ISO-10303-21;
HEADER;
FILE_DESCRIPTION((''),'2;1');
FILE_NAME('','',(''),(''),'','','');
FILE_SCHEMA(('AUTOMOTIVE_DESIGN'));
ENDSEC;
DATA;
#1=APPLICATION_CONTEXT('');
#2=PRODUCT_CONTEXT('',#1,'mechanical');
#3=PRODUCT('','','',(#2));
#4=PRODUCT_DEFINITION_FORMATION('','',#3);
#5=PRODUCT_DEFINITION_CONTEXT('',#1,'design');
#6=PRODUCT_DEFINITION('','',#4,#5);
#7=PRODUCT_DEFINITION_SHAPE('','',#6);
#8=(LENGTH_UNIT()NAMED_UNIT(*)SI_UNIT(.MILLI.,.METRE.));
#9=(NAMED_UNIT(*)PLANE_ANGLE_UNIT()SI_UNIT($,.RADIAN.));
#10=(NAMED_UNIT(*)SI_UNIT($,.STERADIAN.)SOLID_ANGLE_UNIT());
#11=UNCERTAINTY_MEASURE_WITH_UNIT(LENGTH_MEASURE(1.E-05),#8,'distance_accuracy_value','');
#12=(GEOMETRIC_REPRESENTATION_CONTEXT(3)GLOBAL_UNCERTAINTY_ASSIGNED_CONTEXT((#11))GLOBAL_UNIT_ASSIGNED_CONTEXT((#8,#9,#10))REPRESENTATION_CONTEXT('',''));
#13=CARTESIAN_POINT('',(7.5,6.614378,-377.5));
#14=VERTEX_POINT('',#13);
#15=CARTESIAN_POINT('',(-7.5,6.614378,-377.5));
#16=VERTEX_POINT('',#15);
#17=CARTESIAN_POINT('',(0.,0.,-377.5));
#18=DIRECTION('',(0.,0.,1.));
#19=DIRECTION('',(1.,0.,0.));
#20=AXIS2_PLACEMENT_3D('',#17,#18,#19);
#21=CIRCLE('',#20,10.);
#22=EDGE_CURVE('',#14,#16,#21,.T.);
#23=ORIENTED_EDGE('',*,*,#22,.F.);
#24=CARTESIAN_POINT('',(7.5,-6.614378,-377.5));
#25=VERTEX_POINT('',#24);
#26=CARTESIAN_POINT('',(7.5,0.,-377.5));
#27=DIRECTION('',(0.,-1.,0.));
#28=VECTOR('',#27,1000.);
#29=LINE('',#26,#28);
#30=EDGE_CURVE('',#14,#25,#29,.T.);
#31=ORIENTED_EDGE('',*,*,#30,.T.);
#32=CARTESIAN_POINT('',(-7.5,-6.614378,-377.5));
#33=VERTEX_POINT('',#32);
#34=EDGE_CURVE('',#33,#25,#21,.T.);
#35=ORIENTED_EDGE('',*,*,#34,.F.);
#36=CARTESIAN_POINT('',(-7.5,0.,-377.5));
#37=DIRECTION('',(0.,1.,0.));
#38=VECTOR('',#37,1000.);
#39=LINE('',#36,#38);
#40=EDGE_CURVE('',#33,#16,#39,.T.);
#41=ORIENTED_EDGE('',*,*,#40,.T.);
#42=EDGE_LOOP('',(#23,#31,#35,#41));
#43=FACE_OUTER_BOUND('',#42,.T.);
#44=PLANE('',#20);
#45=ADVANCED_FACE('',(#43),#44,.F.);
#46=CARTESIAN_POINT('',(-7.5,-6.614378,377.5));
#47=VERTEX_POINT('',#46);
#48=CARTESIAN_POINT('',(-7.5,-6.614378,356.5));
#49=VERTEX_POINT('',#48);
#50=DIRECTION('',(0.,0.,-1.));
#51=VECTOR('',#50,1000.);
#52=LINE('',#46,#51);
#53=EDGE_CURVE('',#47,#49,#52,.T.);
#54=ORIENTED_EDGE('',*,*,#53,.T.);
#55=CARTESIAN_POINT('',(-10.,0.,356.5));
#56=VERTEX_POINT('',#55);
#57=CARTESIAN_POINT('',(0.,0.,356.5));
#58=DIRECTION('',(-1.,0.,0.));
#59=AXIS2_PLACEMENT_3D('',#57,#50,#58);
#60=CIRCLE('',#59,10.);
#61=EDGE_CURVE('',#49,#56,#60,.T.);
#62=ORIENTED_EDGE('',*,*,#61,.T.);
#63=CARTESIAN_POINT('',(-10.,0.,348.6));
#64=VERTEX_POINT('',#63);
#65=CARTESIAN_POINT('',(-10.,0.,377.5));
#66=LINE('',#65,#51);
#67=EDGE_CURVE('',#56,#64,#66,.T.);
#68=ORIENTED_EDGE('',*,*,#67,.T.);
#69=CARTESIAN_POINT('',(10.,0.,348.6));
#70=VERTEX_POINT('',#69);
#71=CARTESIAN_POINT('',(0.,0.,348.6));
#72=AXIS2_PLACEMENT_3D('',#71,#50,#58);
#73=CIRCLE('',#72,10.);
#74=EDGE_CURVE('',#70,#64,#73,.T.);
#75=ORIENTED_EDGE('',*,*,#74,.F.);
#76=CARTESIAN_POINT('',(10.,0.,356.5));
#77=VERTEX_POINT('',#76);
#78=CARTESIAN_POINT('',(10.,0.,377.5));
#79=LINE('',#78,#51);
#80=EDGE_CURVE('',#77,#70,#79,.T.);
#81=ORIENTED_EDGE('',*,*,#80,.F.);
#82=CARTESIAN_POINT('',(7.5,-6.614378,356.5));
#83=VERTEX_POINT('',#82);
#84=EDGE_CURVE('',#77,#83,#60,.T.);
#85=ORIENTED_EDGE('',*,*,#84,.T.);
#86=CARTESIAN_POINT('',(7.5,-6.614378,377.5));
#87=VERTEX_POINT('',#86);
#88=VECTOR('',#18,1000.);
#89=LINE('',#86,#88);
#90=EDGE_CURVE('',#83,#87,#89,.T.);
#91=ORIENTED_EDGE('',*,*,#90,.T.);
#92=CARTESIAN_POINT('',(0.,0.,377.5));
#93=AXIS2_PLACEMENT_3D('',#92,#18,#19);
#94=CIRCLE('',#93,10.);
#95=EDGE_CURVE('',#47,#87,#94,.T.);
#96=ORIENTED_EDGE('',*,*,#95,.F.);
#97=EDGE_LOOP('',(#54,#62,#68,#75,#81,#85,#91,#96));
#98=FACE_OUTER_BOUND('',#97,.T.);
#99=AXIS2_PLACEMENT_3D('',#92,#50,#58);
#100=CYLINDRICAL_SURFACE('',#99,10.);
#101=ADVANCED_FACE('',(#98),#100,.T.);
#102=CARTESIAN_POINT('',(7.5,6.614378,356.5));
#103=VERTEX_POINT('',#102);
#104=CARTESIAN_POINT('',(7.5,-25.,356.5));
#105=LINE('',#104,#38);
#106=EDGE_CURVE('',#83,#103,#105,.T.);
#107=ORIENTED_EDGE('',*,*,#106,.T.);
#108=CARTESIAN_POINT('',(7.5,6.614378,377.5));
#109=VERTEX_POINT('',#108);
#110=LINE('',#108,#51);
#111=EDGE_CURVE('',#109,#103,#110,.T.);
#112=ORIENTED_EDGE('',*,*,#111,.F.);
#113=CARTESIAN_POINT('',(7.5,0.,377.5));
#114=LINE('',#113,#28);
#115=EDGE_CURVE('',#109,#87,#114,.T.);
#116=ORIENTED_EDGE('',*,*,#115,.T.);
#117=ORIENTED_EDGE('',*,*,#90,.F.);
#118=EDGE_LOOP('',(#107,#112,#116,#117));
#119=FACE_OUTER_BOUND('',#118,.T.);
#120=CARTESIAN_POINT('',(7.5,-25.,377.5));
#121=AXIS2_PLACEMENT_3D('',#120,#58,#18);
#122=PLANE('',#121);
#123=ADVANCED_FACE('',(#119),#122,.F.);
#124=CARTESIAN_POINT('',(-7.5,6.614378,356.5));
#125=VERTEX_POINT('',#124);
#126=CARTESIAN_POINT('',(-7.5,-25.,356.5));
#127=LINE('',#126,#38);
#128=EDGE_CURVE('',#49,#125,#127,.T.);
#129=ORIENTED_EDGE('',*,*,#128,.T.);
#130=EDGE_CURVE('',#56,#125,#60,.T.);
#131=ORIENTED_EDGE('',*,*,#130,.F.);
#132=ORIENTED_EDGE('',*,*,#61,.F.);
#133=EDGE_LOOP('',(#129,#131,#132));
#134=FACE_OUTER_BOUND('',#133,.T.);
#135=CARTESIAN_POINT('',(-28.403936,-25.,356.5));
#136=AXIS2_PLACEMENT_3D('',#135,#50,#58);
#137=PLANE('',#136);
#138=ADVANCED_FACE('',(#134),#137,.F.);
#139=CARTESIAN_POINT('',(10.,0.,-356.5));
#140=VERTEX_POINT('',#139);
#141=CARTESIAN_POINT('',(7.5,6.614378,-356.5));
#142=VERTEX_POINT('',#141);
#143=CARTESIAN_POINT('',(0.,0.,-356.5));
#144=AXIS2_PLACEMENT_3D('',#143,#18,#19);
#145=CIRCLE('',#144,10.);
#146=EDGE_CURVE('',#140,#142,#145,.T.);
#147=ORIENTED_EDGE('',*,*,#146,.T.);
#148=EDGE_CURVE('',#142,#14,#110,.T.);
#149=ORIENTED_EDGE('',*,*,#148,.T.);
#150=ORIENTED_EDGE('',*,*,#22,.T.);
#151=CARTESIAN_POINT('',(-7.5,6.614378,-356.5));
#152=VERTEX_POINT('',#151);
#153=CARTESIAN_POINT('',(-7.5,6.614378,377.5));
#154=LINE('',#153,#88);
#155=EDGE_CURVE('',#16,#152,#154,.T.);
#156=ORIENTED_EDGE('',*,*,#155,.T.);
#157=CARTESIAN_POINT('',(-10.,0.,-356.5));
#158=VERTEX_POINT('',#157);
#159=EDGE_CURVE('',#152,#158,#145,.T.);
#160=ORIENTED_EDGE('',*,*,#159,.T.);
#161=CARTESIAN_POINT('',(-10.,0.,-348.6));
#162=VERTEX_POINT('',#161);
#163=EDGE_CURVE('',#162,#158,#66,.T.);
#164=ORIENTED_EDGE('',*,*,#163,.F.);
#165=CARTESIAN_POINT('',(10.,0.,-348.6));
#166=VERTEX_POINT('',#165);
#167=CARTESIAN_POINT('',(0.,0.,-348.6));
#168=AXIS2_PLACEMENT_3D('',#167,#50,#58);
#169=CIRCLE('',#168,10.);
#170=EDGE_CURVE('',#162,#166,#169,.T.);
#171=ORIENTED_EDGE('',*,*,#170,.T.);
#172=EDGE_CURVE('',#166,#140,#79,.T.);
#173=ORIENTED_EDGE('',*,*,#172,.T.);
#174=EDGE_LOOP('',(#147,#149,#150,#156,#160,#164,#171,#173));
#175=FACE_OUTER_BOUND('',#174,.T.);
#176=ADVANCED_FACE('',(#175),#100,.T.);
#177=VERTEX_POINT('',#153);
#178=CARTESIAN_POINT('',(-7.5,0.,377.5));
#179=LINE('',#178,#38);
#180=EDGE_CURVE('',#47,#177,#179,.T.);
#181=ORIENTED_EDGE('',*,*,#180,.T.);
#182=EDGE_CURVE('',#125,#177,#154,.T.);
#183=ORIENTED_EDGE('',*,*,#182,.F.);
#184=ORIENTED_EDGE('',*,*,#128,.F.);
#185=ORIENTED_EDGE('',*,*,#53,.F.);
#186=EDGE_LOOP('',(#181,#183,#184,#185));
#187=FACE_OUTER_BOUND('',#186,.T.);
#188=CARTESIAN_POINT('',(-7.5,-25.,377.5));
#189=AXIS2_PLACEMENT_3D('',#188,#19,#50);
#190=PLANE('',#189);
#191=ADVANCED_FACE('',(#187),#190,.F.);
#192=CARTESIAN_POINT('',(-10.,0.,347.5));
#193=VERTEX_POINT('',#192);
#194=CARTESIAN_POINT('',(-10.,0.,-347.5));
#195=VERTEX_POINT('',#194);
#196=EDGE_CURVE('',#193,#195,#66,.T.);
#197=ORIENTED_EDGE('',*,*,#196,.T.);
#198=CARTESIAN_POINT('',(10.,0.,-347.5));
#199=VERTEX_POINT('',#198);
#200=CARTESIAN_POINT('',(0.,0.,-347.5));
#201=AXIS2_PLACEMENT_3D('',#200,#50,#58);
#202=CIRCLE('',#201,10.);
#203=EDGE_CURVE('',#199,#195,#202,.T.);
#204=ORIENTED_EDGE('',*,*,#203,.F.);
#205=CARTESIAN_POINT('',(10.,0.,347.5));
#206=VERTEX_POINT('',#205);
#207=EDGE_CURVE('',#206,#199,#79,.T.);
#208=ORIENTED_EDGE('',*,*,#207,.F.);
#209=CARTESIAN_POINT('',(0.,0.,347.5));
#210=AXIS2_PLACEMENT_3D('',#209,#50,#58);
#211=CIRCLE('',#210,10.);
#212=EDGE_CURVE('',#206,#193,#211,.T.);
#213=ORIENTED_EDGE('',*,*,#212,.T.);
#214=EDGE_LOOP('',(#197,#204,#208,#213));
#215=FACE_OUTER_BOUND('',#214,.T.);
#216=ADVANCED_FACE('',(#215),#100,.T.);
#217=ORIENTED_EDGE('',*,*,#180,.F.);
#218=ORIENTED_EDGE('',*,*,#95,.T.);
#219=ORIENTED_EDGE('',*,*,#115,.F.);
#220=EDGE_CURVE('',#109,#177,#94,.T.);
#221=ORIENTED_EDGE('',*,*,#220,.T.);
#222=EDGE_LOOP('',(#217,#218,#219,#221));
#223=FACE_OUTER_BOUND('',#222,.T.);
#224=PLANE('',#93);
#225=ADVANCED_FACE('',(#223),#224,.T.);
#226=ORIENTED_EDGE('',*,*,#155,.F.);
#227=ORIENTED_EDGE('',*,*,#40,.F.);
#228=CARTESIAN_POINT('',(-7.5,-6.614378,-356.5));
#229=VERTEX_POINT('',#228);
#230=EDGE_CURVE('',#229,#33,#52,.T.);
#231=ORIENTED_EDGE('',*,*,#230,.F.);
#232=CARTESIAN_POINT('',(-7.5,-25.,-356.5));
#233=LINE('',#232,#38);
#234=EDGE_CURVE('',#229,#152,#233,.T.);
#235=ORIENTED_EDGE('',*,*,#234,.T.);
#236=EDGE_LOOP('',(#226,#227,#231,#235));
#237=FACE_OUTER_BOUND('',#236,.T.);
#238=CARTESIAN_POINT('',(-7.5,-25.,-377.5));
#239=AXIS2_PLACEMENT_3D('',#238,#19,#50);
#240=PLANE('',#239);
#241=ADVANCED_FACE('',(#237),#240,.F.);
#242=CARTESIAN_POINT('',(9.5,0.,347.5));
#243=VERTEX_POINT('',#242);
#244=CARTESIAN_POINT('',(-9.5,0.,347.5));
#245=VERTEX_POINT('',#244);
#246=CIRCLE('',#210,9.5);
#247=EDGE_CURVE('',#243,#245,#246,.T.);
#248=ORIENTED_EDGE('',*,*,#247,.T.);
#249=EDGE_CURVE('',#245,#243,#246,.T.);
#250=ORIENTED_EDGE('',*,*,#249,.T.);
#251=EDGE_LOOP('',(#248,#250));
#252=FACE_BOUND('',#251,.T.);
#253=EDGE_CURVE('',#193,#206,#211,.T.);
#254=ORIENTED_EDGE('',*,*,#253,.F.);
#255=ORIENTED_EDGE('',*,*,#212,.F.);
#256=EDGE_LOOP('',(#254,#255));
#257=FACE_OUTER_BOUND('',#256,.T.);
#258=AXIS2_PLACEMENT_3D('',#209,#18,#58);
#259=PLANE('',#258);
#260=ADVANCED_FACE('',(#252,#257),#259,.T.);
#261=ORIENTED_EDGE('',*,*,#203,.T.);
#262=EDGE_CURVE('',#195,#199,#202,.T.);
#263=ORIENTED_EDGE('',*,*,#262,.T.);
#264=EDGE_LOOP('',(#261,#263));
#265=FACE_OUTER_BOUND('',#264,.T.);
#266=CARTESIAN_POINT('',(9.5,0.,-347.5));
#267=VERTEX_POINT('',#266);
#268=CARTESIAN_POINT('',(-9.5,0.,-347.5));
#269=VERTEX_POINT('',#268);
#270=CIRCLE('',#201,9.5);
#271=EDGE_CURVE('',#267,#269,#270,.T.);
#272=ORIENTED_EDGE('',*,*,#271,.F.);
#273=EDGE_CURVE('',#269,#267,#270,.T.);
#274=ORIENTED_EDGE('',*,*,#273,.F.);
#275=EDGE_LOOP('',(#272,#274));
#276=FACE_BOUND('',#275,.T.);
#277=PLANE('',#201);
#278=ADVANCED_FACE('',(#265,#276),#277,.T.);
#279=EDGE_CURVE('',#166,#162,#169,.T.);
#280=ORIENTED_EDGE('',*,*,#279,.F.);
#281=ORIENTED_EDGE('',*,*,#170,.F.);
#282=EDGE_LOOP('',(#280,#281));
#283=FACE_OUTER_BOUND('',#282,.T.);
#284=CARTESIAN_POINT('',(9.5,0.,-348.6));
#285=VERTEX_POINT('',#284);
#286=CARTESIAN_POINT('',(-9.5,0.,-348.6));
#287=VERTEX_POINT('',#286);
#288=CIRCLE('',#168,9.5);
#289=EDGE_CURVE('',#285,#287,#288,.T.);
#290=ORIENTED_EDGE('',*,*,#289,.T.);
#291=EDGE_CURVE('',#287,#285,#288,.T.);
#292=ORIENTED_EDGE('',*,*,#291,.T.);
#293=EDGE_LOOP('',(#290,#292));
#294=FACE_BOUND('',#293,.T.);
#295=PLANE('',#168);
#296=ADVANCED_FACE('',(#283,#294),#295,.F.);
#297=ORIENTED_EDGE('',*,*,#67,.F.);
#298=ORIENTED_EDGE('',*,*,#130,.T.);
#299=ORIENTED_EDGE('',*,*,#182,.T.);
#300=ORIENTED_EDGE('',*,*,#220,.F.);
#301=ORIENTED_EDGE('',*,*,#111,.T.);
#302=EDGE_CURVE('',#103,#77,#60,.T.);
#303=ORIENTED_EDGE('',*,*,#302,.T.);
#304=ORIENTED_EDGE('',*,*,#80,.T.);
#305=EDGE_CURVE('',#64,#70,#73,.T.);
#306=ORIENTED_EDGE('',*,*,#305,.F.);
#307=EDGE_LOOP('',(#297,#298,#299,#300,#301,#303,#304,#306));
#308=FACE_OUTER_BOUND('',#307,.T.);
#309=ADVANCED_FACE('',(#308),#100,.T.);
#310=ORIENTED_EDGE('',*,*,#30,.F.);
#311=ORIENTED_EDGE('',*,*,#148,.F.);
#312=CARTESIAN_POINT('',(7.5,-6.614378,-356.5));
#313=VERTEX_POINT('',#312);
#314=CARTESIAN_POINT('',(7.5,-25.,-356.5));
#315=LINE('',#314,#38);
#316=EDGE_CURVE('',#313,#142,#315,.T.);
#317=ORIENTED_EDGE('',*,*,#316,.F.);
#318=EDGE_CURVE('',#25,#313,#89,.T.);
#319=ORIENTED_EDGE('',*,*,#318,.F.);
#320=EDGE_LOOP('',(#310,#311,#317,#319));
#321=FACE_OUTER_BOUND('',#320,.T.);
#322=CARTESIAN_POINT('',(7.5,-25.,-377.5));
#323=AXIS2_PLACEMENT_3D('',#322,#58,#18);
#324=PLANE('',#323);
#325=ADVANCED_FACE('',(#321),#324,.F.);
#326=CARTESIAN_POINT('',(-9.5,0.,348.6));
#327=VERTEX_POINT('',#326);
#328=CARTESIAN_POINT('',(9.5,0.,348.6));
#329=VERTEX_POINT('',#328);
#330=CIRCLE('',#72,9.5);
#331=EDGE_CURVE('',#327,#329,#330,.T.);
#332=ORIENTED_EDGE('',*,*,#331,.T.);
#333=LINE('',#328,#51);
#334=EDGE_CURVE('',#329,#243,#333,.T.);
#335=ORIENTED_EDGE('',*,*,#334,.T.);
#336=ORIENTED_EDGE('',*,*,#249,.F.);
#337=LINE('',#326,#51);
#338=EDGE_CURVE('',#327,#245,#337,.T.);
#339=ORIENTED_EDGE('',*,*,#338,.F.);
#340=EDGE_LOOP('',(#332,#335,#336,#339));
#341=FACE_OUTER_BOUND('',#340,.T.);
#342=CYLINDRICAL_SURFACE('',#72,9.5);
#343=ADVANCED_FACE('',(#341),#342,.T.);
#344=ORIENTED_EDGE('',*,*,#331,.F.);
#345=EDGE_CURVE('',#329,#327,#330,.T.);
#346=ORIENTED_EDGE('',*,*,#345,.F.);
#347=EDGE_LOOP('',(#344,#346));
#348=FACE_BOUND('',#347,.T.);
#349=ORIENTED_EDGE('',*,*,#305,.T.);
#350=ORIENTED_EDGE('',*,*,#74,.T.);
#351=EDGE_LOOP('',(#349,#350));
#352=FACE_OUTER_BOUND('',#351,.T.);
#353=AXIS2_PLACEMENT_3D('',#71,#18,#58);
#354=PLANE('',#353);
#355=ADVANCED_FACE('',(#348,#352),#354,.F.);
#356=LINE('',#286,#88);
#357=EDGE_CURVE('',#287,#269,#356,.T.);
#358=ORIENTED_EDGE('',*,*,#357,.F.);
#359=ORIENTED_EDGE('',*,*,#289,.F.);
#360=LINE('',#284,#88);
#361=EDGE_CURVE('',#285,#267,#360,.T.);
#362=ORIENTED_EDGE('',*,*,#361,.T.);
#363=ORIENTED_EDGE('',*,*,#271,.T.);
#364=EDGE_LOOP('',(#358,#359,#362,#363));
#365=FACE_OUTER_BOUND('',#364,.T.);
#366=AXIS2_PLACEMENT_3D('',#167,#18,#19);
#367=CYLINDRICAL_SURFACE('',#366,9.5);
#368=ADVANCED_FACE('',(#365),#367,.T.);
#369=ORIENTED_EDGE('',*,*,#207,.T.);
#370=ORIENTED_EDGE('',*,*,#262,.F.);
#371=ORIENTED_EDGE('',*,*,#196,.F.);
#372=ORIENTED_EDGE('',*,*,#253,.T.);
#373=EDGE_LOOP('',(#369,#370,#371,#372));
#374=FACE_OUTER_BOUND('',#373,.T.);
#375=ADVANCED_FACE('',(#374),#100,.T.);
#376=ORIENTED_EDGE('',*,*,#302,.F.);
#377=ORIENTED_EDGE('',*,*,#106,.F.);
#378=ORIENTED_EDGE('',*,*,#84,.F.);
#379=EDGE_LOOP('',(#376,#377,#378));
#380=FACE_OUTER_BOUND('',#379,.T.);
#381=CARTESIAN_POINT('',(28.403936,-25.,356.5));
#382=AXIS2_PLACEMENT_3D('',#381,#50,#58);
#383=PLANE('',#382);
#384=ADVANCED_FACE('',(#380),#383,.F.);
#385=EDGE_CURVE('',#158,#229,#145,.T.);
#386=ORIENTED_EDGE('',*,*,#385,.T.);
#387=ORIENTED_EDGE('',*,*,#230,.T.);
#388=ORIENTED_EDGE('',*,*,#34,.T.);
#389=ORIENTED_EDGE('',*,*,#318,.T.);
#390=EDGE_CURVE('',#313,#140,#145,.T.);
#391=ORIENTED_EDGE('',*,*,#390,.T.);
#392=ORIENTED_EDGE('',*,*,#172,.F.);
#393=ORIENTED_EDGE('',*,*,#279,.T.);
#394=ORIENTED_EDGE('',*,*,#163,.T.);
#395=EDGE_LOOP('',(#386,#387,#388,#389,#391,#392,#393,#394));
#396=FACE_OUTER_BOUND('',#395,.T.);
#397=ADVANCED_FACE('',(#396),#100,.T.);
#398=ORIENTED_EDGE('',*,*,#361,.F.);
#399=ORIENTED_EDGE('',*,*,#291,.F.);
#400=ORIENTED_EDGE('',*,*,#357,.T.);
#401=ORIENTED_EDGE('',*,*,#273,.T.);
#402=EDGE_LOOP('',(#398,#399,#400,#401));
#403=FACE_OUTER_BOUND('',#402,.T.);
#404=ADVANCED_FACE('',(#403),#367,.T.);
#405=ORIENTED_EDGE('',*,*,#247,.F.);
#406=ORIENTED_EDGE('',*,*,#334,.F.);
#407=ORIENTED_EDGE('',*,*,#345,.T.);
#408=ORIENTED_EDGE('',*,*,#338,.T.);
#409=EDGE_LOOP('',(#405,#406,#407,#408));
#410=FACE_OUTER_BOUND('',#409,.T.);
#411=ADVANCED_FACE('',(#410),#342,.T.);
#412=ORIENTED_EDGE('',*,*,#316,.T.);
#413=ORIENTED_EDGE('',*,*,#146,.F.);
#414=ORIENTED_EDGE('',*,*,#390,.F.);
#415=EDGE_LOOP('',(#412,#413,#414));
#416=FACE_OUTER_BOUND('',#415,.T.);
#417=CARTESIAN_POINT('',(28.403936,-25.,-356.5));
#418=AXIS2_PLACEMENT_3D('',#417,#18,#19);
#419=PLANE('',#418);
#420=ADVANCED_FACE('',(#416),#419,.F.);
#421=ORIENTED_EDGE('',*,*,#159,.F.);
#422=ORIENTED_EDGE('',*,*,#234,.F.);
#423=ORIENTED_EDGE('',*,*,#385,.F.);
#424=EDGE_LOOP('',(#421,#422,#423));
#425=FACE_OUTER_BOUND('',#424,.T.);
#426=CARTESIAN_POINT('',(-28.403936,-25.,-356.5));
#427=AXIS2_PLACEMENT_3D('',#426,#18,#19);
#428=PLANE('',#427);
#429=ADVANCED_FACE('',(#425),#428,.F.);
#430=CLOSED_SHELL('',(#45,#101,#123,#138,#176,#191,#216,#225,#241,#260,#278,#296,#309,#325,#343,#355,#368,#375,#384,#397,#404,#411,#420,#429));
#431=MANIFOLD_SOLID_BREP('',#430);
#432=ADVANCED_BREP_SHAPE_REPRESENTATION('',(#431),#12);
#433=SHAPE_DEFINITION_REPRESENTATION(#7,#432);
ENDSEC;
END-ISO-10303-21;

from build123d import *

# Parameters (mm, degrees)
SKETCH_1_R          = 10
EXTRUDE_1_DEPTH     = 377.5
SKETCH_2_W          = 20.903935991
SKETCH_2_H          = 21
CUT_EXTRUDE_1_DEPTH = 25
CUT_EXTRUDE_START   = -30
SKETCH_5_R          = 10
SKETCH_5_R_2        = 9.5
CUT_EXTRUDE_2_DEPTH = 1.1


with BuildPart() as part:
    # 草图1 → 凸台-拉伸1 (new, symmetric)
    with BuildSketch(Plane.XY):
        Circle(SKETCH_1_R)
    extrude(amount=EXTRUDE_1_DEPTH, both=True)

    # 草图2 → 切除-拉伸1 (cut, symmetric)
    with BuildSketch(Plane(origin=(0, 0, 0), x_dir=(1, 0, 0), z_dir=(0, 1, 0))):
        with Locations((-17.951967996, 367)):
            Rectangle(SKETCH_2_W, SKETCH_2_H)
        with Locations((17.951967996, 367)):
            Rectangle(SKETCH_2_W, SKETCH_2_H)
        with Locations((17.951967996, -367)):
            Rectangle(SKETCH_2_W, SKETCH_2_H)
        with Locations((-17.951967996, -367)):
            Rectangle(SKETCH_2_W, SKETCH_2_H)
    extrude(amount=CUT_EXTRUDE_1_DEPTH, both=True, mode=Mode.SUBTRACT)

    # 草图5 → 切除-拉伸2 (cut)
    with BuildSketch(Plane(origin=(0, 0, -377.5), x_dir=(-1, 0, 0), z_dir=(0, 0, -1)).offset(CUT_EXTRUDE_START)):
        Circle(SKETCH_5_R)
        Circle(SKETCH_5_R_2, mode=Mode.SUBTRACT)
    cut_extrude_2 = extrude(amount=CUT_EXTRUDE_2_DEPTH, mode=Mode.SUBTRACT)

    # 镜向1: 切除-拉伸2 across plane
    add(cut_extrude_2.mirror(Plane.XY), mode=Mode.SUBTRACT)


solid = part.part
